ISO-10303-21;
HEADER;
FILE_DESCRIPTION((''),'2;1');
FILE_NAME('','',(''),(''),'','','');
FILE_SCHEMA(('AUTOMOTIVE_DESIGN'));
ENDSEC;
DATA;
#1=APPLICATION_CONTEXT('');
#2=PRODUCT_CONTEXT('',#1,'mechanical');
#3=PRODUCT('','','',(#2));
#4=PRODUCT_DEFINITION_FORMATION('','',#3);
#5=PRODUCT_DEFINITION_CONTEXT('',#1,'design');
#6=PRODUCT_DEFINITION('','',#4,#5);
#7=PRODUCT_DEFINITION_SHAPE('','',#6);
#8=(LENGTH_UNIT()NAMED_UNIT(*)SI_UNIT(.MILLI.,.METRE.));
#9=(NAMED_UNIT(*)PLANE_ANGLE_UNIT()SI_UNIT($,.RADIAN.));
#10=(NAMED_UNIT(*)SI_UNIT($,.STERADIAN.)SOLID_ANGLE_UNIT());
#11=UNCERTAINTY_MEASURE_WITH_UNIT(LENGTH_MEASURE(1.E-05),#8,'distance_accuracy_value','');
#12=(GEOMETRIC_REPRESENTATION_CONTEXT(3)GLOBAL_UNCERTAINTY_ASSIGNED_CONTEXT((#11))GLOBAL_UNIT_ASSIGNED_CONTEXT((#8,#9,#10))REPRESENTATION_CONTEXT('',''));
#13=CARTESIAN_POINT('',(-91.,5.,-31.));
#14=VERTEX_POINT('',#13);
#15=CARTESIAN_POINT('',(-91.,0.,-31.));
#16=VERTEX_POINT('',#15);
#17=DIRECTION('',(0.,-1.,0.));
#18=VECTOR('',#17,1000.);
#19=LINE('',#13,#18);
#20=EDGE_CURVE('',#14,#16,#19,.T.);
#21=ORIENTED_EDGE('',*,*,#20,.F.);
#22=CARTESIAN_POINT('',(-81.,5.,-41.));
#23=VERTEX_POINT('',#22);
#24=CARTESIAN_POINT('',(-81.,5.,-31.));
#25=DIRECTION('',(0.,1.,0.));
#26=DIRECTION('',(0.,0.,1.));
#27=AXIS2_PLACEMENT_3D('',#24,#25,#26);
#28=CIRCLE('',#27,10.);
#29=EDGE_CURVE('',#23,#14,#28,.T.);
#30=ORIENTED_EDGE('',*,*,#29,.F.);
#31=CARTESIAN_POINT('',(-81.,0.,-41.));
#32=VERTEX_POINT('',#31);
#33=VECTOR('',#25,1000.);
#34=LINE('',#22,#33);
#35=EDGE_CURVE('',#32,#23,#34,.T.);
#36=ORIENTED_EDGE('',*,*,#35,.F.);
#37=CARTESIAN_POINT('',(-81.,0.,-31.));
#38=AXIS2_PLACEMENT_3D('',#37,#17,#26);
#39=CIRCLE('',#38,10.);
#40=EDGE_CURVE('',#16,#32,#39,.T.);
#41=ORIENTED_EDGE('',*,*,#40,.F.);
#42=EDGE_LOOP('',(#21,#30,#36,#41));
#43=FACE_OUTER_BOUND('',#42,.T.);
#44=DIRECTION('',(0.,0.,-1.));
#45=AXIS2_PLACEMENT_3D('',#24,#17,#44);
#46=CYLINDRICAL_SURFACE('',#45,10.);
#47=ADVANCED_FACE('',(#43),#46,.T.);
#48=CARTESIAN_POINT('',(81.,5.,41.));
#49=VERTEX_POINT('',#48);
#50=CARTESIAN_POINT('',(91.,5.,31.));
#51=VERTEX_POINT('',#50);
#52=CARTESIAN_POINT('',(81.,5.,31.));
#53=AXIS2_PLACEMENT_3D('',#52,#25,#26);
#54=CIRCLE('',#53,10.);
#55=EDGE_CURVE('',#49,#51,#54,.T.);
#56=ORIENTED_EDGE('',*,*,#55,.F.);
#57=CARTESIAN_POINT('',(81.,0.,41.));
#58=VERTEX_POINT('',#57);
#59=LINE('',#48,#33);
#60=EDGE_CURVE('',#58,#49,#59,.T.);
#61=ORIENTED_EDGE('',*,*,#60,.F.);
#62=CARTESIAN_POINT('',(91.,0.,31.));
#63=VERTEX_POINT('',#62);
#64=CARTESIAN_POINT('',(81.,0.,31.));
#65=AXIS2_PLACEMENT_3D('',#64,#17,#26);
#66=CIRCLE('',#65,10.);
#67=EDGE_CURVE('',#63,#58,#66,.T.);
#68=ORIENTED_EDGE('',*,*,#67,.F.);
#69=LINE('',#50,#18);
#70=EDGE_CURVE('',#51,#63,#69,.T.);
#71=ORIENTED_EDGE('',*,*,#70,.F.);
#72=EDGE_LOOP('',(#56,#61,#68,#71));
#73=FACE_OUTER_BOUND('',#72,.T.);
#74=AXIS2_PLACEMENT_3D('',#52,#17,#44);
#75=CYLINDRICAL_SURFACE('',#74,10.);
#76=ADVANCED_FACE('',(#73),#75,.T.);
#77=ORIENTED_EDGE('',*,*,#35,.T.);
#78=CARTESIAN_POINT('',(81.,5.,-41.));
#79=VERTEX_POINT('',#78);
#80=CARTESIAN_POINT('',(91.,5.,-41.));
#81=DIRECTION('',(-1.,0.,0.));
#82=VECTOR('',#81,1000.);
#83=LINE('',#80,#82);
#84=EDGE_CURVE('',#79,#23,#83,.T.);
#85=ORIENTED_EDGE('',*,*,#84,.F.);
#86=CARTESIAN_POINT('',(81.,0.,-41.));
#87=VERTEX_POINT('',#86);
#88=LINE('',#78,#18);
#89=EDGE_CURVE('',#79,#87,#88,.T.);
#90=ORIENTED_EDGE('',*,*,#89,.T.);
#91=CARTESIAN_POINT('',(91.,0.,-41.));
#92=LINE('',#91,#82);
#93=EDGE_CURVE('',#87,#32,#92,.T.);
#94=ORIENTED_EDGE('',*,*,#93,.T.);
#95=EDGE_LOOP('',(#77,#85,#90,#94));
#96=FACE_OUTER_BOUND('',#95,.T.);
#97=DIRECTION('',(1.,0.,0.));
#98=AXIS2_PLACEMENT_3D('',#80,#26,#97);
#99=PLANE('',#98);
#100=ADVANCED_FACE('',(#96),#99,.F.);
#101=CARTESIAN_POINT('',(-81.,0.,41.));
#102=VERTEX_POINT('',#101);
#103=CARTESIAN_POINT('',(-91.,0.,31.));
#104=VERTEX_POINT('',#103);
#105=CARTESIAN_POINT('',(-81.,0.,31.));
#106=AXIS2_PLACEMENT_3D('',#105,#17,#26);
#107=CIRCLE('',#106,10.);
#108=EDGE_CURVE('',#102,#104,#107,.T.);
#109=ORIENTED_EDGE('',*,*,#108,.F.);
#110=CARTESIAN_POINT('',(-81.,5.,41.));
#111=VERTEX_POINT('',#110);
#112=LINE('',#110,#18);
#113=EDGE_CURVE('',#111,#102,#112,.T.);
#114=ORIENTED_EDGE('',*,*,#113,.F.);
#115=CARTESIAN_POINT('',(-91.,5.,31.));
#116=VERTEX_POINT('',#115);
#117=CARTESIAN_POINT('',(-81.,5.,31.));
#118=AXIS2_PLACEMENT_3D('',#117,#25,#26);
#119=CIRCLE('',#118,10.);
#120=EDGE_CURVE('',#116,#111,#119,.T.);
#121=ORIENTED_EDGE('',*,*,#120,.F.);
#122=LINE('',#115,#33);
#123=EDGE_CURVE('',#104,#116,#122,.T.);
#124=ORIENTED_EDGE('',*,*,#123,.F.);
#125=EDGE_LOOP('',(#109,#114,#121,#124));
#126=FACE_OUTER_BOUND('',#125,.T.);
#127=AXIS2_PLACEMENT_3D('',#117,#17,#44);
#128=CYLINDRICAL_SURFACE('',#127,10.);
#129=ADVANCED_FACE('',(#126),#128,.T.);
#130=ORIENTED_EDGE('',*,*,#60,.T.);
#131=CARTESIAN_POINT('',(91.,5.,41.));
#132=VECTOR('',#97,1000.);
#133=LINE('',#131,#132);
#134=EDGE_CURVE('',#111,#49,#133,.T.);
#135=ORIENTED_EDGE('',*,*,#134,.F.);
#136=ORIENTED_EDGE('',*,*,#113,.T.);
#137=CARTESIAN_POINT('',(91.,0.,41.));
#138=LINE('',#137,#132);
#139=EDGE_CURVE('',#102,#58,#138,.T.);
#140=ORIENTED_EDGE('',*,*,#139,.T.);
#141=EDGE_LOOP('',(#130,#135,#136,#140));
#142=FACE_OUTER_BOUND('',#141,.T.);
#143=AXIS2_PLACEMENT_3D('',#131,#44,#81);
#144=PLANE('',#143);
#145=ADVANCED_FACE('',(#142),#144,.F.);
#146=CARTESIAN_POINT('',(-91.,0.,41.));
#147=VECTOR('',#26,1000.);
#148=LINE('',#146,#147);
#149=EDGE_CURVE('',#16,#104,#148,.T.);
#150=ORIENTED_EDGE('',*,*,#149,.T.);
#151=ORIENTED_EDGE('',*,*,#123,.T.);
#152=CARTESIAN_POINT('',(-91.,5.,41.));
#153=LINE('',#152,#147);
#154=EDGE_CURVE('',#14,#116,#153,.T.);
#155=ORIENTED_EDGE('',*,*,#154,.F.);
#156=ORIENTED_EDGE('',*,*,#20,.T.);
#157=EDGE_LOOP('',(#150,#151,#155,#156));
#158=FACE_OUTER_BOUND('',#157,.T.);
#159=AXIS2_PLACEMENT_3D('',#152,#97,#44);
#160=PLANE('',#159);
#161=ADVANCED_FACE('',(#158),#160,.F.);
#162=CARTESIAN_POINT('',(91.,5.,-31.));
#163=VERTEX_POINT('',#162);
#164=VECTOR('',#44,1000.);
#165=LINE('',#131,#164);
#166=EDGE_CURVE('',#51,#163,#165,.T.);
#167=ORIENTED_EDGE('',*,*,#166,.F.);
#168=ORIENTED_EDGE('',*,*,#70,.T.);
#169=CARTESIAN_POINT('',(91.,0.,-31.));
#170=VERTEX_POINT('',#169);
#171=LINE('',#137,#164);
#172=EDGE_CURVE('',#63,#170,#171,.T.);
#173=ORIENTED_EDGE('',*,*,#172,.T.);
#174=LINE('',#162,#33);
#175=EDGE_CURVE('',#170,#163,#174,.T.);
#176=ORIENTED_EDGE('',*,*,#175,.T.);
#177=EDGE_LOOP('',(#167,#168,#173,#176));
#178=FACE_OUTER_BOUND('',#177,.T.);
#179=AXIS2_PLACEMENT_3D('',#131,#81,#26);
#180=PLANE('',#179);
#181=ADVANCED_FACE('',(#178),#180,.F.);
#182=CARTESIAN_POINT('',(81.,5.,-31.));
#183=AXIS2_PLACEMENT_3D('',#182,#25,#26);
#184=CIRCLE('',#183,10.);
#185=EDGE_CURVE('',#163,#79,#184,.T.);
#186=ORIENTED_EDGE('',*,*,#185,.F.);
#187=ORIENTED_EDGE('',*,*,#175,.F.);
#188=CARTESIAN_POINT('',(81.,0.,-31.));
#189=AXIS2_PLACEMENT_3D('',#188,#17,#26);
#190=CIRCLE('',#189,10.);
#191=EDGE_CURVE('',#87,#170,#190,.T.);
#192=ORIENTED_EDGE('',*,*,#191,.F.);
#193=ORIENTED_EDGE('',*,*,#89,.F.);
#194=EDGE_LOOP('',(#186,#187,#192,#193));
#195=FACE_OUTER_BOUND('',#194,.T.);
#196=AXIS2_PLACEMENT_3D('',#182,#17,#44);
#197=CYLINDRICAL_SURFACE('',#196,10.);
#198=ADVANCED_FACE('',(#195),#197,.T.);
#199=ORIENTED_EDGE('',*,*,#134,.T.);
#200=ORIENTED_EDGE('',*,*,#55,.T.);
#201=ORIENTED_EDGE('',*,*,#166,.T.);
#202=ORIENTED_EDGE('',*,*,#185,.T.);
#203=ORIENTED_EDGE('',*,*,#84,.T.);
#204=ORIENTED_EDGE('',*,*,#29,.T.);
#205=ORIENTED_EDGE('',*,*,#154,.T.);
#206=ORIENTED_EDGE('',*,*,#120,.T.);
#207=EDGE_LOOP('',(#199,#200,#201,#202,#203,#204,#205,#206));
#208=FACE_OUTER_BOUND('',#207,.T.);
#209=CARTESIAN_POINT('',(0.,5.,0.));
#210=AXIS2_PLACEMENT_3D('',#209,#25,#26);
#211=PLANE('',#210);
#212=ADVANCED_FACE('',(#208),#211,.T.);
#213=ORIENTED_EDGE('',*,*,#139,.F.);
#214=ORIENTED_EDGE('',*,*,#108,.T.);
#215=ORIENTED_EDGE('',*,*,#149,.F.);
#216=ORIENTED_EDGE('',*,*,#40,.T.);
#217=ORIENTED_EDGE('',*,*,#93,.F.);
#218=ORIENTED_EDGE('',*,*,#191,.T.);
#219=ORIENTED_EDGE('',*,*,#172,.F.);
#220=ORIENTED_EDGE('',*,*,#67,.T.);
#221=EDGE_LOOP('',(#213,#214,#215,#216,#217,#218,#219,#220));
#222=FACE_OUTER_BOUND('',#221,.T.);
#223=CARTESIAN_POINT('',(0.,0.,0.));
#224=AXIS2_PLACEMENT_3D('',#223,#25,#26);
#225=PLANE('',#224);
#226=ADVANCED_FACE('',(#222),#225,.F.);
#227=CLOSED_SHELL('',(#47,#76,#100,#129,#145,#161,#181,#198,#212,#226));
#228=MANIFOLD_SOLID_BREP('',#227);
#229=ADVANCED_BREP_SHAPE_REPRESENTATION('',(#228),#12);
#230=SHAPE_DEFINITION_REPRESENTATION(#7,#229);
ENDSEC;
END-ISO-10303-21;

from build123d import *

# Parameters (mm, degrees)
SKETCH1_W           = 182
SKETCH1_H           = 82
BOSS_EXTRUDE1_DEPTH = 5
FILLET1_R           = 10


with BuildPart() as part:
    # Sketch1 → Boss-Extrude1 (new body)
    with BuildSketch(Plane(origin=(0, 0, 0), x_dir=(1, 0, 0), z_dir=(0, 1, 0))):
        Rectangle(SKETCH1_W, SKETCH1_H)
    extrude(amount=BOSS_EXTRUDE1_DEPTH)

    # Fillet1
    fillet1_edges = [part.edges().sort_by_distance(p)[0] for p in [
        (-91, 2.5, -41),
        (91, 2.5, -41),
        (91, 2.5, 41),
        (-91, 2.5, 41),
    ]]
    fillet(fillet1_edges, radius=FILLET1_R)


solid = part.part
